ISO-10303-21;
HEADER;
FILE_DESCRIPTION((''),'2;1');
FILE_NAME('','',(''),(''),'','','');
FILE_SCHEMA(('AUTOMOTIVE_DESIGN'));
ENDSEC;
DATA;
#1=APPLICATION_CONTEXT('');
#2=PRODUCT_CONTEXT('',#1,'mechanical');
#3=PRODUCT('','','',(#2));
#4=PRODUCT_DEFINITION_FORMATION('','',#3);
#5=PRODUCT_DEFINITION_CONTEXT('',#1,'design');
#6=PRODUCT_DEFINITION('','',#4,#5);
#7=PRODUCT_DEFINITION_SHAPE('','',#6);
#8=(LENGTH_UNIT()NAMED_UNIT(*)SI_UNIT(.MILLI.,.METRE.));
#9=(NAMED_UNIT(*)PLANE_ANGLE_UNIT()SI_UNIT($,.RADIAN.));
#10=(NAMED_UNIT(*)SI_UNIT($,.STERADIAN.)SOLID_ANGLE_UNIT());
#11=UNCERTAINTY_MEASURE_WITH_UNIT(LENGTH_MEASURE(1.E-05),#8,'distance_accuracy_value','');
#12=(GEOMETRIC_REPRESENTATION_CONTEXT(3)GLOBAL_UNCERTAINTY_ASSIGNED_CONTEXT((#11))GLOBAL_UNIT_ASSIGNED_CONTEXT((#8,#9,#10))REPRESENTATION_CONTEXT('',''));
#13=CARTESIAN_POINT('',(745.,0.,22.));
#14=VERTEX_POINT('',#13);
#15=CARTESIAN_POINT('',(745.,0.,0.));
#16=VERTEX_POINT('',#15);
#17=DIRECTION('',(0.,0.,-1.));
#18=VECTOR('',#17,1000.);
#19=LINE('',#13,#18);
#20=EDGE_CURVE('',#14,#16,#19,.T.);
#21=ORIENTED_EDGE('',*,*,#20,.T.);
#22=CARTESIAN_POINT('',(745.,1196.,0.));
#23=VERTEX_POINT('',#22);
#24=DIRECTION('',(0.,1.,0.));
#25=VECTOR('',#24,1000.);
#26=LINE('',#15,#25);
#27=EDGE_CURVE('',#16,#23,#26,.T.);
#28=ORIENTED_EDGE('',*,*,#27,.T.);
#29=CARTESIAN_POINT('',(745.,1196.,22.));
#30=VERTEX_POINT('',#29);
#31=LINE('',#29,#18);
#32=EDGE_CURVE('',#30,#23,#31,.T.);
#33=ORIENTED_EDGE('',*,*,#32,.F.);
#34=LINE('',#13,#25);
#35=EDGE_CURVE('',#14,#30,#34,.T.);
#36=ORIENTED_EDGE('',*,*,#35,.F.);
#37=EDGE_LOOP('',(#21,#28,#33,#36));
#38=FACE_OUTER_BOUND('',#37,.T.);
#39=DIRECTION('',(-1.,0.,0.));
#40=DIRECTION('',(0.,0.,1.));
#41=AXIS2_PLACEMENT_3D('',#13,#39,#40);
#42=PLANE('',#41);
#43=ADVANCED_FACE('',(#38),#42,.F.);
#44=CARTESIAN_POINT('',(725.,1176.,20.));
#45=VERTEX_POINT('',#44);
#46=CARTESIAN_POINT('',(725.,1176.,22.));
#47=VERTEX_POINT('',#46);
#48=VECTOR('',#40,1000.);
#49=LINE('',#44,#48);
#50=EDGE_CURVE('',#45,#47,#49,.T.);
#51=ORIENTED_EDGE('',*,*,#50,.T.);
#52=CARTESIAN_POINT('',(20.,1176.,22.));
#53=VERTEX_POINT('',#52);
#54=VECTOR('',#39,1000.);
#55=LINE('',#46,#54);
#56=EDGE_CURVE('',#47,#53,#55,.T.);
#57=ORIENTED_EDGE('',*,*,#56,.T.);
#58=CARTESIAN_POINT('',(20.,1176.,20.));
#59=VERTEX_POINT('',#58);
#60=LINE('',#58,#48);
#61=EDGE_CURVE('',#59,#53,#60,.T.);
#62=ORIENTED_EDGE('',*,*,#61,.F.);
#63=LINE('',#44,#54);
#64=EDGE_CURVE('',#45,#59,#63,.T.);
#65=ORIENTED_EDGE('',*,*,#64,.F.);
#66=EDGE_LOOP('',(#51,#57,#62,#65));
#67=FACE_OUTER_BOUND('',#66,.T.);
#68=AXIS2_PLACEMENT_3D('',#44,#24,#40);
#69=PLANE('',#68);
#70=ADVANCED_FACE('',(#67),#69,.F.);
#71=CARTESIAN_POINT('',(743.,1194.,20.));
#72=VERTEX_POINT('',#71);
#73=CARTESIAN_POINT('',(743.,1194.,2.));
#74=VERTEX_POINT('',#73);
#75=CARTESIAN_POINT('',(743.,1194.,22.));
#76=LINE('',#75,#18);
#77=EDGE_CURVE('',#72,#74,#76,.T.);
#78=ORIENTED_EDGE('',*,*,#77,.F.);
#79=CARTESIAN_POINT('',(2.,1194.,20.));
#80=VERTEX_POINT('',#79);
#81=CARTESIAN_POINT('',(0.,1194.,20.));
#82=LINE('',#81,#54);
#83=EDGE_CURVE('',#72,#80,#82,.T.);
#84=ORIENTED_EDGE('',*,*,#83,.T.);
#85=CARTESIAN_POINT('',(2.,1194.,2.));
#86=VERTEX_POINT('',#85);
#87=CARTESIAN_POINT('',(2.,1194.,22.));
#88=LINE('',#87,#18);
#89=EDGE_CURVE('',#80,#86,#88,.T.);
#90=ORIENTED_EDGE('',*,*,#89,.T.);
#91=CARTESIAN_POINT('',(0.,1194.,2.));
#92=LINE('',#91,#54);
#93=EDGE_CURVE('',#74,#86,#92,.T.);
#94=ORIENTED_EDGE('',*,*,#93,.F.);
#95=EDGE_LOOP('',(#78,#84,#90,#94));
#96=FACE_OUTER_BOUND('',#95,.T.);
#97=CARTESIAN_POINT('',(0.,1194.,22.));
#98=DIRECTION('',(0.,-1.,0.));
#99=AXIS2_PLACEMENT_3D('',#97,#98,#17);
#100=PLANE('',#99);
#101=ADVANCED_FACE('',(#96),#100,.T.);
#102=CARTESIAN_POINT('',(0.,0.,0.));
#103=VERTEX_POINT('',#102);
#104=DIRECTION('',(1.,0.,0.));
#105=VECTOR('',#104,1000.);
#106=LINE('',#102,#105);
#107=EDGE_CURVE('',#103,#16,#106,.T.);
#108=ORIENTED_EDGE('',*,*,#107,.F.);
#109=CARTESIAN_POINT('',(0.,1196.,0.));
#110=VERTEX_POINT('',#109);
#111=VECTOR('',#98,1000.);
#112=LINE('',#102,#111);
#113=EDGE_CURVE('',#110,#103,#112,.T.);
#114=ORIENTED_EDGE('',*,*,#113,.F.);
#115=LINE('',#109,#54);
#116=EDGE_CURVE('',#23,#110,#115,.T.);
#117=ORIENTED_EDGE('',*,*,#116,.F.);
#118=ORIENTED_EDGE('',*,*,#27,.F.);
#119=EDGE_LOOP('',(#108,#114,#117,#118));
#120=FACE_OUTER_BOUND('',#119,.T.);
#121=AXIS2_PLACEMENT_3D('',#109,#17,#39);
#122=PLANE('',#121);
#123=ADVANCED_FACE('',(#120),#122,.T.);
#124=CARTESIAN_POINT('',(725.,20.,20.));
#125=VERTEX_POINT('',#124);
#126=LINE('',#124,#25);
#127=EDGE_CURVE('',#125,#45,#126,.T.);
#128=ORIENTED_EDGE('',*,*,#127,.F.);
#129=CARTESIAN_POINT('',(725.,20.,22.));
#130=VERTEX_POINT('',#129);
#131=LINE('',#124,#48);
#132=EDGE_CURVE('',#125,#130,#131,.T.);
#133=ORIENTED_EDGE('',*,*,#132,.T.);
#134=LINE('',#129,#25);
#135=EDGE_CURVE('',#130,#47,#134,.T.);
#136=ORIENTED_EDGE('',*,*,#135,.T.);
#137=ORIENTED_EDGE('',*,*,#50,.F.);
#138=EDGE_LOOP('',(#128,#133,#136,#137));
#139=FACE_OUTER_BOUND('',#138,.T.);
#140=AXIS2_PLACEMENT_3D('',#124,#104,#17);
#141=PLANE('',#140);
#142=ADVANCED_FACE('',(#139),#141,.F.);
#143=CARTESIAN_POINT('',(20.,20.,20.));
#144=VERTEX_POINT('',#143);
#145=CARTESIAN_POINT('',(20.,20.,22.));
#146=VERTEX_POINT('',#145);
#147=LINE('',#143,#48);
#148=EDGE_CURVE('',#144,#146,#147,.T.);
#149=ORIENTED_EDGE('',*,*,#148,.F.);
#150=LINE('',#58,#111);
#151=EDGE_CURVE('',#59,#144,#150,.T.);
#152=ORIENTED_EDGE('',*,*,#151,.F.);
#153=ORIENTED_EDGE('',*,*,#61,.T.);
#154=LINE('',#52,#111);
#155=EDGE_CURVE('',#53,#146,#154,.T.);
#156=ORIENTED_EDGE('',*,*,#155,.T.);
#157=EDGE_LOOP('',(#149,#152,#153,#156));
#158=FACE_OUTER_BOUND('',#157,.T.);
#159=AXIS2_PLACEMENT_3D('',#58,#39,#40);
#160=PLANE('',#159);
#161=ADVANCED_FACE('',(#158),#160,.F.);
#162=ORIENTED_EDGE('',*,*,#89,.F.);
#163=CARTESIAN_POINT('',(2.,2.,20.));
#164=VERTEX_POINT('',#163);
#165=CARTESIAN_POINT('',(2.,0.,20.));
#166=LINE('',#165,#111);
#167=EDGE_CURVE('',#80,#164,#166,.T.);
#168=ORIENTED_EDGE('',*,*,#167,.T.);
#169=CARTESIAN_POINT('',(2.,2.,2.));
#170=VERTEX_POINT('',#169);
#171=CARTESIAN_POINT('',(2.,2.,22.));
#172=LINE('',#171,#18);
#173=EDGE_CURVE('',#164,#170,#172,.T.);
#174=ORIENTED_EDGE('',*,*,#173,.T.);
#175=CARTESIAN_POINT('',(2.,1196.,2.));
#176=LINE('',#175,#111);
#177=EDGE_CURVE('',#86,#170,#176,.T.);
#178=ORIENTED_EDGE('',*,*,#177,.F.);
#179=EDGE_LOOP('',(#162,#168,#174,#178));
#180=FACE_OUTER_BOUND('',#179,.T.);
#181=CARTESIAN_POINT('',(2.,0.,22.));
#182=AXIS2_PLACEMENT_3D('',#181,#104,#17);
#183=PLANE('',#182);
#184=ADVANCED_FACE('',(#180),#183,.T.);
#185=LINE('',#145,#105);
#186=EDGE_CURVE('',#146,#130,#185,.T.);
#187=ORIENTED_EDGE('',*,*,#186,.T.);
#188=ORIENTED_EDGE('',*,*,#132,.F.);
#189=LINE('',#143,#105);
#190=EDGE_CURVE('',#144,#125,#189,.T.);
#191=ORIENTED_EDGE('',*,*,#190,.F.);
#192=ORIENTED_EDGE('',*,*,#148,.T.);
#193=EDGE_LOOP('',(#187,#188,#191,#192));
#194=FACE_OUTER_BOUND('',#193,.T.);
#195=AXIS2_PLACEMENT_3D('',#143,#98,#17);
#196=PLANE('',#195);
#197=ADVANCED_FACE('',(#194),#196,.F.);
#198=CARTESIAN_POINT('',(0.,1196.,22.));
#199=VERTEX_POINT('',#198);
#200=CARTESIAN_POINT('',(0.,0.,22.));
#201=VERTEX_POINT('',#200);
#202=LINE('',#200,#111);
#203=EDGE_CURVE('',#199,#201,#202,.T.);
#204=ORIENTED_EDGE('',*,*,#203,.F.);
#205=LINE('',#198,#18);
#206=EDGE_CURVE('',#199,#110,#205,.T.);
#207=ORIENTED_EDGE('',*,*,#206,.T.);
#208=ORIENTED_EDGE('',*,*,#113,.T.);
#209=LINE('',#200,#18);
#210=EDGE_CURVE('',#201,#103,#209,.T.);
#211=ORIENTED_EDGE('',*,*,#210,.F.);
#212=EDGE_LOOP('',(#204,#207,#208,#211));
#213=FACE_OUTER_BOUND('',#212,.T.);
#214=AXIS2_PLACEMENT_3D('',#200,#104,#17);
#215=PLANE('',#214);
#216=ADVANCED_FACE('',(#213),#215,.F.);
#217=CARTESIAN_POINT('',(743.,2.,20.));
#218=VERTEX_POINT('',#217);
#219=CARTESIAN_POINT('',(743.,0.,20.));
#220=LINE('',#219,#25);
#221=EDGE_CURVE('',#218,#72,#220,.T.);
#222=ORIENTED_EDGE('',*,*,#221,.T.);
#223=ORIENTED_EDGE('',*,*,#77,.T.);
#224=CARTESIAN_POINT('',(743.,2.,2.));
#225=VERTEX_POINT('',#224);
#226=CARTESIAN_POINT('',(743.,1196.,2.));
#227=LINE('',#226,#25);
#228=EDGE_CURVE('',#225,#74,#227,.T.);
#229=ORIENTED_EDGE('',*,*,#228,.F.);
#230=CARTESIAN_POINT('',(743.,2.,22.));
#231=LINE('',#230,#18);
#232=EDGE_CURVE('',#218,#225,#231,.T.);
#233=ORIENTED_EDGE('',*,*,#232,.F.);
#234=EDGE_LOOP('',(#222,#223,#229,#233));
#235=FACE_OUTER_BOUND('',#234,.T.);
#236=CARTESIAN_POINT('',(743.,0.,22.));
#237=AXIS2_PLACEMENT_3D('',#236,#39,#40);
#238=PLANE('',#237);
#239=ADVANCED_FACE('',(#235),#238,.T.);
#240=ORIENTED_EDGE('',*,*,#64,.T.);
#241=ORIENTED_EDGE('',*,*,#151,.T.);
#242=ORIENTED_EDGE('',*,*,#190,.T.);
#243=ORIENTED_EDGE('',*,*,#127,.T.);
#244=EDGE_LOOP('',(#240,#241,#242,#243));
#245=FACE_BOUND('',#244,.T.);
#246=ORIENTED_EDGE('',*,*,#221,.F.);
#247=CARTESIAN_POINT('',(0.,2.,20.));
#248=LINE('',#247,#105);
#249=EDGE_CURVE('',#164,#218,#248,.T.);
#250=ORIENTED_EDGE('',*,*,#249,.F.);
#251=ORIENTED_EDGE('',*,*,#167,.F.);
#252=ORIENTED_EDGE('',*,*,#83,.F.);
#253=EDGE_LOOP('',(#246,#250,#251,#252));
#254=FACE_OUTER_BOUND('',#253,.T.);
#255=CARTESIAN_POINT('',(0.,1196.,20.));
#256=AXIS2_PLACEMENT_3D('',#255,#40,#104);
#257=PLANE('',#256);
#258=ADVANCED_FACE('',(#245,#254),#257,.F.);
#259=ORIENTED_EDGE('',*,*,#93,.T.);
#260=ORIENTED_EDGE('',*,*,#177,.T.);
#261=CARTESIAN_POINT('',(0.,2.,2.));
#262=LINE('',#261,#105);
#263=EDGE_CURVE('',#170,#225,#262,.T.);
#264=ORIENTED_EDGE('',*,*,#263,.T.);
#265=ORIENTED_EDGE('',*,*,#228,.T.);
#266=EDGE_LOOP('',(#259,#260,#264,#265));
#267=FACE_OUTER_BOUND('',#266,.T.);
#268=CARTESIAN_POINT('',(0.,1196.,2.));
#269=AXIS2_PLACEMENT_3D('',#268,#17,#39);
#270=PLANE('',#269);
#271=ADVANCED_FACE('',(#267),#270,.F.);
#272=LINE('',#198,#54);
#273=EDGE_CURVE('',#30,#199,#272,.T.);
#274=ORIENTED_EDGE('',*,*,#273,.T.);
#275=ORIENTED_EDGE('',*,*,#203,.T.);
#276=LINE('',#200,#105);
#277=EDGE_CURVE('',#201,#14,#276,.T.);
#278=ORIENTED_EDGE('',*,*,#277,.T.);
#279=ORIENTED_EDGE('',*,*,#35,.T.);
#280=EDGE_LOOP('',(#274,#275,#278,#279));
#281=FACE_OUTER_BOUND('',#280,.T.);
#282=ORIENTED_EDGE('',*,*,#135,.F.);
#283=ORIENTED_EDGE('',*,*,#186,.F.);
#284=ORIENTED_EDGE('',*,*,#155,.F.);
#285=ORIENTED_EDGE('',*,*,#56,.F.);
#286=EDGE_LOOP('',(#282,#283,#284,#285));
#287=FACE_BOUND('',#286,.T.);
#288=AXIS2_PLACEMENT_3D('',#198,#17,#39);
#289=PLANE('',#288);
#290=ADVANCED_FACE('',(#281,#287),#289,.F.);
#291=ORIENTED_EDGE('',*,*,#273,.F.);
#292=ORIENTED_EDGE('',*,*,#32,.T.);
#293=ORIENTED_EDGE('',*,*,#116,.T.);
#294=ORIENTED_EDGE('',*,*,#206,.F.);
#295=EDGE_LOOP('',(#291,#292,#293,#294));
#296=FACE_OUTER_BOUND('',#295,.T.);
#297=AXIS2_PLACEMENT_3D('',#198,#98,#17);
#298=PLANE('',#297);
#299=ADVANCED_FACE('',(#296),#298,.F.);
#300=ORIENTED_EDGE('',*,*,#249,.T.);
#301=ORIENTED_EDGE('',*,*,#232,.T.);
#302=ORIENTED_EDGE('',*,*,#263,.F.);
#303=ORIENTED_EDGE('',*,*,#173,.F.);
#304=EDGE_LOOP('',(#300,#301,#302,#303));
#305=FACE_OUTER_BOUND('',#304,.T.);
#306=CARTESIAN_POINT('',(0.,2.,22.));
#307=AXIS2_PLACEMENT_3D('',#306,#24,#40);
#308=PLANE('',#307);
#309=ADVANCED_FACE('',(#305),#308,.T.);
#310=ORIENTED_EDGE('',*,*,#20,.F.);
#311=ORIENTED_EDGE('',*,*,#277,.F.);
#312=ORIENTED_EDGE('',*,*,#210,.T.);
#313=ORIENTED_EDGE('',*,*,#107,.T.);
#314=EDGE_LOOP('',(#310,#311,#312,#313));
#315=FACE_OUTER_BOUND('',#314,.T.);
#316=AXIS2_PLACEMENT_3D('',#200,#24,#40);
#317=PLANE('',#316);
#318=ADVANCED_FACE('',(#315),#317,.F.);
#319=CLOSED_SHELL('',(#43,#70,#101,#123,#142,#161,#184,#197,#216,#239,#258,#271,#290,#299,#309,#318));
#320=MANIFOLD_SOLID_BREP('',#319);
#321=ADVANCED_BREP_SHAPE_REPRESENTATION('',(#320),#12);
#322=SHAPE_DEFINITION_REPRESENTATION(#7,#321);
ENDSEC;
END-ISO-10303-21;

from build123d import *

# Parameters (mm, degrees)
SKETCH_1_W      = 745
SKETCH_1_H      = 1196
EXTRUDE_1_DEPTH = 22
SHELL_1_T       = -2
SKETCH_2_W      = 745
SKETCH_2_H      = 1196
SKETCH_2_W_2    = 705
SKETCH_2_H_2    = 1156
EXTRUDE_2_DEPTH = 2


with BuildPart() as part:
    # 草图1 → 凸台-拉伸1 (new body)
    with BuildSketch(Plane.XY):
        with Locations((372.5, 598)):
            Rectangle(SKETCH_1_W, SKETCH_1_H)
    extrude(amount=EXTRUDE_1_DEPTH)

    # 抽壳1
    shell_1_openings = [part.faces().sort_by_distance(p)[0] for p in [
        (372.5, 598, 22),
    ]]
    offset(amount=SHELL_1_T, openings=shell_1_openings, kind=Kind.INTERSECTION)

    # 草图2 → 凸台-拉伸2 (add)
    with BuildSketch(Plane.XY.offset(22)):
        with Locations((372.5, 598)):
            Rectangle(SKETCH_2_W, SKETCH_2_H)
        with Locations((372.5, 598)):
            Rectangle(SKETCH_2_W_2, SKETCH_2_H_2, mode=Mode.SUBTRACT)
    extrude(amount=-EXTRUDE_2_DEPTH)


solid = part.part
